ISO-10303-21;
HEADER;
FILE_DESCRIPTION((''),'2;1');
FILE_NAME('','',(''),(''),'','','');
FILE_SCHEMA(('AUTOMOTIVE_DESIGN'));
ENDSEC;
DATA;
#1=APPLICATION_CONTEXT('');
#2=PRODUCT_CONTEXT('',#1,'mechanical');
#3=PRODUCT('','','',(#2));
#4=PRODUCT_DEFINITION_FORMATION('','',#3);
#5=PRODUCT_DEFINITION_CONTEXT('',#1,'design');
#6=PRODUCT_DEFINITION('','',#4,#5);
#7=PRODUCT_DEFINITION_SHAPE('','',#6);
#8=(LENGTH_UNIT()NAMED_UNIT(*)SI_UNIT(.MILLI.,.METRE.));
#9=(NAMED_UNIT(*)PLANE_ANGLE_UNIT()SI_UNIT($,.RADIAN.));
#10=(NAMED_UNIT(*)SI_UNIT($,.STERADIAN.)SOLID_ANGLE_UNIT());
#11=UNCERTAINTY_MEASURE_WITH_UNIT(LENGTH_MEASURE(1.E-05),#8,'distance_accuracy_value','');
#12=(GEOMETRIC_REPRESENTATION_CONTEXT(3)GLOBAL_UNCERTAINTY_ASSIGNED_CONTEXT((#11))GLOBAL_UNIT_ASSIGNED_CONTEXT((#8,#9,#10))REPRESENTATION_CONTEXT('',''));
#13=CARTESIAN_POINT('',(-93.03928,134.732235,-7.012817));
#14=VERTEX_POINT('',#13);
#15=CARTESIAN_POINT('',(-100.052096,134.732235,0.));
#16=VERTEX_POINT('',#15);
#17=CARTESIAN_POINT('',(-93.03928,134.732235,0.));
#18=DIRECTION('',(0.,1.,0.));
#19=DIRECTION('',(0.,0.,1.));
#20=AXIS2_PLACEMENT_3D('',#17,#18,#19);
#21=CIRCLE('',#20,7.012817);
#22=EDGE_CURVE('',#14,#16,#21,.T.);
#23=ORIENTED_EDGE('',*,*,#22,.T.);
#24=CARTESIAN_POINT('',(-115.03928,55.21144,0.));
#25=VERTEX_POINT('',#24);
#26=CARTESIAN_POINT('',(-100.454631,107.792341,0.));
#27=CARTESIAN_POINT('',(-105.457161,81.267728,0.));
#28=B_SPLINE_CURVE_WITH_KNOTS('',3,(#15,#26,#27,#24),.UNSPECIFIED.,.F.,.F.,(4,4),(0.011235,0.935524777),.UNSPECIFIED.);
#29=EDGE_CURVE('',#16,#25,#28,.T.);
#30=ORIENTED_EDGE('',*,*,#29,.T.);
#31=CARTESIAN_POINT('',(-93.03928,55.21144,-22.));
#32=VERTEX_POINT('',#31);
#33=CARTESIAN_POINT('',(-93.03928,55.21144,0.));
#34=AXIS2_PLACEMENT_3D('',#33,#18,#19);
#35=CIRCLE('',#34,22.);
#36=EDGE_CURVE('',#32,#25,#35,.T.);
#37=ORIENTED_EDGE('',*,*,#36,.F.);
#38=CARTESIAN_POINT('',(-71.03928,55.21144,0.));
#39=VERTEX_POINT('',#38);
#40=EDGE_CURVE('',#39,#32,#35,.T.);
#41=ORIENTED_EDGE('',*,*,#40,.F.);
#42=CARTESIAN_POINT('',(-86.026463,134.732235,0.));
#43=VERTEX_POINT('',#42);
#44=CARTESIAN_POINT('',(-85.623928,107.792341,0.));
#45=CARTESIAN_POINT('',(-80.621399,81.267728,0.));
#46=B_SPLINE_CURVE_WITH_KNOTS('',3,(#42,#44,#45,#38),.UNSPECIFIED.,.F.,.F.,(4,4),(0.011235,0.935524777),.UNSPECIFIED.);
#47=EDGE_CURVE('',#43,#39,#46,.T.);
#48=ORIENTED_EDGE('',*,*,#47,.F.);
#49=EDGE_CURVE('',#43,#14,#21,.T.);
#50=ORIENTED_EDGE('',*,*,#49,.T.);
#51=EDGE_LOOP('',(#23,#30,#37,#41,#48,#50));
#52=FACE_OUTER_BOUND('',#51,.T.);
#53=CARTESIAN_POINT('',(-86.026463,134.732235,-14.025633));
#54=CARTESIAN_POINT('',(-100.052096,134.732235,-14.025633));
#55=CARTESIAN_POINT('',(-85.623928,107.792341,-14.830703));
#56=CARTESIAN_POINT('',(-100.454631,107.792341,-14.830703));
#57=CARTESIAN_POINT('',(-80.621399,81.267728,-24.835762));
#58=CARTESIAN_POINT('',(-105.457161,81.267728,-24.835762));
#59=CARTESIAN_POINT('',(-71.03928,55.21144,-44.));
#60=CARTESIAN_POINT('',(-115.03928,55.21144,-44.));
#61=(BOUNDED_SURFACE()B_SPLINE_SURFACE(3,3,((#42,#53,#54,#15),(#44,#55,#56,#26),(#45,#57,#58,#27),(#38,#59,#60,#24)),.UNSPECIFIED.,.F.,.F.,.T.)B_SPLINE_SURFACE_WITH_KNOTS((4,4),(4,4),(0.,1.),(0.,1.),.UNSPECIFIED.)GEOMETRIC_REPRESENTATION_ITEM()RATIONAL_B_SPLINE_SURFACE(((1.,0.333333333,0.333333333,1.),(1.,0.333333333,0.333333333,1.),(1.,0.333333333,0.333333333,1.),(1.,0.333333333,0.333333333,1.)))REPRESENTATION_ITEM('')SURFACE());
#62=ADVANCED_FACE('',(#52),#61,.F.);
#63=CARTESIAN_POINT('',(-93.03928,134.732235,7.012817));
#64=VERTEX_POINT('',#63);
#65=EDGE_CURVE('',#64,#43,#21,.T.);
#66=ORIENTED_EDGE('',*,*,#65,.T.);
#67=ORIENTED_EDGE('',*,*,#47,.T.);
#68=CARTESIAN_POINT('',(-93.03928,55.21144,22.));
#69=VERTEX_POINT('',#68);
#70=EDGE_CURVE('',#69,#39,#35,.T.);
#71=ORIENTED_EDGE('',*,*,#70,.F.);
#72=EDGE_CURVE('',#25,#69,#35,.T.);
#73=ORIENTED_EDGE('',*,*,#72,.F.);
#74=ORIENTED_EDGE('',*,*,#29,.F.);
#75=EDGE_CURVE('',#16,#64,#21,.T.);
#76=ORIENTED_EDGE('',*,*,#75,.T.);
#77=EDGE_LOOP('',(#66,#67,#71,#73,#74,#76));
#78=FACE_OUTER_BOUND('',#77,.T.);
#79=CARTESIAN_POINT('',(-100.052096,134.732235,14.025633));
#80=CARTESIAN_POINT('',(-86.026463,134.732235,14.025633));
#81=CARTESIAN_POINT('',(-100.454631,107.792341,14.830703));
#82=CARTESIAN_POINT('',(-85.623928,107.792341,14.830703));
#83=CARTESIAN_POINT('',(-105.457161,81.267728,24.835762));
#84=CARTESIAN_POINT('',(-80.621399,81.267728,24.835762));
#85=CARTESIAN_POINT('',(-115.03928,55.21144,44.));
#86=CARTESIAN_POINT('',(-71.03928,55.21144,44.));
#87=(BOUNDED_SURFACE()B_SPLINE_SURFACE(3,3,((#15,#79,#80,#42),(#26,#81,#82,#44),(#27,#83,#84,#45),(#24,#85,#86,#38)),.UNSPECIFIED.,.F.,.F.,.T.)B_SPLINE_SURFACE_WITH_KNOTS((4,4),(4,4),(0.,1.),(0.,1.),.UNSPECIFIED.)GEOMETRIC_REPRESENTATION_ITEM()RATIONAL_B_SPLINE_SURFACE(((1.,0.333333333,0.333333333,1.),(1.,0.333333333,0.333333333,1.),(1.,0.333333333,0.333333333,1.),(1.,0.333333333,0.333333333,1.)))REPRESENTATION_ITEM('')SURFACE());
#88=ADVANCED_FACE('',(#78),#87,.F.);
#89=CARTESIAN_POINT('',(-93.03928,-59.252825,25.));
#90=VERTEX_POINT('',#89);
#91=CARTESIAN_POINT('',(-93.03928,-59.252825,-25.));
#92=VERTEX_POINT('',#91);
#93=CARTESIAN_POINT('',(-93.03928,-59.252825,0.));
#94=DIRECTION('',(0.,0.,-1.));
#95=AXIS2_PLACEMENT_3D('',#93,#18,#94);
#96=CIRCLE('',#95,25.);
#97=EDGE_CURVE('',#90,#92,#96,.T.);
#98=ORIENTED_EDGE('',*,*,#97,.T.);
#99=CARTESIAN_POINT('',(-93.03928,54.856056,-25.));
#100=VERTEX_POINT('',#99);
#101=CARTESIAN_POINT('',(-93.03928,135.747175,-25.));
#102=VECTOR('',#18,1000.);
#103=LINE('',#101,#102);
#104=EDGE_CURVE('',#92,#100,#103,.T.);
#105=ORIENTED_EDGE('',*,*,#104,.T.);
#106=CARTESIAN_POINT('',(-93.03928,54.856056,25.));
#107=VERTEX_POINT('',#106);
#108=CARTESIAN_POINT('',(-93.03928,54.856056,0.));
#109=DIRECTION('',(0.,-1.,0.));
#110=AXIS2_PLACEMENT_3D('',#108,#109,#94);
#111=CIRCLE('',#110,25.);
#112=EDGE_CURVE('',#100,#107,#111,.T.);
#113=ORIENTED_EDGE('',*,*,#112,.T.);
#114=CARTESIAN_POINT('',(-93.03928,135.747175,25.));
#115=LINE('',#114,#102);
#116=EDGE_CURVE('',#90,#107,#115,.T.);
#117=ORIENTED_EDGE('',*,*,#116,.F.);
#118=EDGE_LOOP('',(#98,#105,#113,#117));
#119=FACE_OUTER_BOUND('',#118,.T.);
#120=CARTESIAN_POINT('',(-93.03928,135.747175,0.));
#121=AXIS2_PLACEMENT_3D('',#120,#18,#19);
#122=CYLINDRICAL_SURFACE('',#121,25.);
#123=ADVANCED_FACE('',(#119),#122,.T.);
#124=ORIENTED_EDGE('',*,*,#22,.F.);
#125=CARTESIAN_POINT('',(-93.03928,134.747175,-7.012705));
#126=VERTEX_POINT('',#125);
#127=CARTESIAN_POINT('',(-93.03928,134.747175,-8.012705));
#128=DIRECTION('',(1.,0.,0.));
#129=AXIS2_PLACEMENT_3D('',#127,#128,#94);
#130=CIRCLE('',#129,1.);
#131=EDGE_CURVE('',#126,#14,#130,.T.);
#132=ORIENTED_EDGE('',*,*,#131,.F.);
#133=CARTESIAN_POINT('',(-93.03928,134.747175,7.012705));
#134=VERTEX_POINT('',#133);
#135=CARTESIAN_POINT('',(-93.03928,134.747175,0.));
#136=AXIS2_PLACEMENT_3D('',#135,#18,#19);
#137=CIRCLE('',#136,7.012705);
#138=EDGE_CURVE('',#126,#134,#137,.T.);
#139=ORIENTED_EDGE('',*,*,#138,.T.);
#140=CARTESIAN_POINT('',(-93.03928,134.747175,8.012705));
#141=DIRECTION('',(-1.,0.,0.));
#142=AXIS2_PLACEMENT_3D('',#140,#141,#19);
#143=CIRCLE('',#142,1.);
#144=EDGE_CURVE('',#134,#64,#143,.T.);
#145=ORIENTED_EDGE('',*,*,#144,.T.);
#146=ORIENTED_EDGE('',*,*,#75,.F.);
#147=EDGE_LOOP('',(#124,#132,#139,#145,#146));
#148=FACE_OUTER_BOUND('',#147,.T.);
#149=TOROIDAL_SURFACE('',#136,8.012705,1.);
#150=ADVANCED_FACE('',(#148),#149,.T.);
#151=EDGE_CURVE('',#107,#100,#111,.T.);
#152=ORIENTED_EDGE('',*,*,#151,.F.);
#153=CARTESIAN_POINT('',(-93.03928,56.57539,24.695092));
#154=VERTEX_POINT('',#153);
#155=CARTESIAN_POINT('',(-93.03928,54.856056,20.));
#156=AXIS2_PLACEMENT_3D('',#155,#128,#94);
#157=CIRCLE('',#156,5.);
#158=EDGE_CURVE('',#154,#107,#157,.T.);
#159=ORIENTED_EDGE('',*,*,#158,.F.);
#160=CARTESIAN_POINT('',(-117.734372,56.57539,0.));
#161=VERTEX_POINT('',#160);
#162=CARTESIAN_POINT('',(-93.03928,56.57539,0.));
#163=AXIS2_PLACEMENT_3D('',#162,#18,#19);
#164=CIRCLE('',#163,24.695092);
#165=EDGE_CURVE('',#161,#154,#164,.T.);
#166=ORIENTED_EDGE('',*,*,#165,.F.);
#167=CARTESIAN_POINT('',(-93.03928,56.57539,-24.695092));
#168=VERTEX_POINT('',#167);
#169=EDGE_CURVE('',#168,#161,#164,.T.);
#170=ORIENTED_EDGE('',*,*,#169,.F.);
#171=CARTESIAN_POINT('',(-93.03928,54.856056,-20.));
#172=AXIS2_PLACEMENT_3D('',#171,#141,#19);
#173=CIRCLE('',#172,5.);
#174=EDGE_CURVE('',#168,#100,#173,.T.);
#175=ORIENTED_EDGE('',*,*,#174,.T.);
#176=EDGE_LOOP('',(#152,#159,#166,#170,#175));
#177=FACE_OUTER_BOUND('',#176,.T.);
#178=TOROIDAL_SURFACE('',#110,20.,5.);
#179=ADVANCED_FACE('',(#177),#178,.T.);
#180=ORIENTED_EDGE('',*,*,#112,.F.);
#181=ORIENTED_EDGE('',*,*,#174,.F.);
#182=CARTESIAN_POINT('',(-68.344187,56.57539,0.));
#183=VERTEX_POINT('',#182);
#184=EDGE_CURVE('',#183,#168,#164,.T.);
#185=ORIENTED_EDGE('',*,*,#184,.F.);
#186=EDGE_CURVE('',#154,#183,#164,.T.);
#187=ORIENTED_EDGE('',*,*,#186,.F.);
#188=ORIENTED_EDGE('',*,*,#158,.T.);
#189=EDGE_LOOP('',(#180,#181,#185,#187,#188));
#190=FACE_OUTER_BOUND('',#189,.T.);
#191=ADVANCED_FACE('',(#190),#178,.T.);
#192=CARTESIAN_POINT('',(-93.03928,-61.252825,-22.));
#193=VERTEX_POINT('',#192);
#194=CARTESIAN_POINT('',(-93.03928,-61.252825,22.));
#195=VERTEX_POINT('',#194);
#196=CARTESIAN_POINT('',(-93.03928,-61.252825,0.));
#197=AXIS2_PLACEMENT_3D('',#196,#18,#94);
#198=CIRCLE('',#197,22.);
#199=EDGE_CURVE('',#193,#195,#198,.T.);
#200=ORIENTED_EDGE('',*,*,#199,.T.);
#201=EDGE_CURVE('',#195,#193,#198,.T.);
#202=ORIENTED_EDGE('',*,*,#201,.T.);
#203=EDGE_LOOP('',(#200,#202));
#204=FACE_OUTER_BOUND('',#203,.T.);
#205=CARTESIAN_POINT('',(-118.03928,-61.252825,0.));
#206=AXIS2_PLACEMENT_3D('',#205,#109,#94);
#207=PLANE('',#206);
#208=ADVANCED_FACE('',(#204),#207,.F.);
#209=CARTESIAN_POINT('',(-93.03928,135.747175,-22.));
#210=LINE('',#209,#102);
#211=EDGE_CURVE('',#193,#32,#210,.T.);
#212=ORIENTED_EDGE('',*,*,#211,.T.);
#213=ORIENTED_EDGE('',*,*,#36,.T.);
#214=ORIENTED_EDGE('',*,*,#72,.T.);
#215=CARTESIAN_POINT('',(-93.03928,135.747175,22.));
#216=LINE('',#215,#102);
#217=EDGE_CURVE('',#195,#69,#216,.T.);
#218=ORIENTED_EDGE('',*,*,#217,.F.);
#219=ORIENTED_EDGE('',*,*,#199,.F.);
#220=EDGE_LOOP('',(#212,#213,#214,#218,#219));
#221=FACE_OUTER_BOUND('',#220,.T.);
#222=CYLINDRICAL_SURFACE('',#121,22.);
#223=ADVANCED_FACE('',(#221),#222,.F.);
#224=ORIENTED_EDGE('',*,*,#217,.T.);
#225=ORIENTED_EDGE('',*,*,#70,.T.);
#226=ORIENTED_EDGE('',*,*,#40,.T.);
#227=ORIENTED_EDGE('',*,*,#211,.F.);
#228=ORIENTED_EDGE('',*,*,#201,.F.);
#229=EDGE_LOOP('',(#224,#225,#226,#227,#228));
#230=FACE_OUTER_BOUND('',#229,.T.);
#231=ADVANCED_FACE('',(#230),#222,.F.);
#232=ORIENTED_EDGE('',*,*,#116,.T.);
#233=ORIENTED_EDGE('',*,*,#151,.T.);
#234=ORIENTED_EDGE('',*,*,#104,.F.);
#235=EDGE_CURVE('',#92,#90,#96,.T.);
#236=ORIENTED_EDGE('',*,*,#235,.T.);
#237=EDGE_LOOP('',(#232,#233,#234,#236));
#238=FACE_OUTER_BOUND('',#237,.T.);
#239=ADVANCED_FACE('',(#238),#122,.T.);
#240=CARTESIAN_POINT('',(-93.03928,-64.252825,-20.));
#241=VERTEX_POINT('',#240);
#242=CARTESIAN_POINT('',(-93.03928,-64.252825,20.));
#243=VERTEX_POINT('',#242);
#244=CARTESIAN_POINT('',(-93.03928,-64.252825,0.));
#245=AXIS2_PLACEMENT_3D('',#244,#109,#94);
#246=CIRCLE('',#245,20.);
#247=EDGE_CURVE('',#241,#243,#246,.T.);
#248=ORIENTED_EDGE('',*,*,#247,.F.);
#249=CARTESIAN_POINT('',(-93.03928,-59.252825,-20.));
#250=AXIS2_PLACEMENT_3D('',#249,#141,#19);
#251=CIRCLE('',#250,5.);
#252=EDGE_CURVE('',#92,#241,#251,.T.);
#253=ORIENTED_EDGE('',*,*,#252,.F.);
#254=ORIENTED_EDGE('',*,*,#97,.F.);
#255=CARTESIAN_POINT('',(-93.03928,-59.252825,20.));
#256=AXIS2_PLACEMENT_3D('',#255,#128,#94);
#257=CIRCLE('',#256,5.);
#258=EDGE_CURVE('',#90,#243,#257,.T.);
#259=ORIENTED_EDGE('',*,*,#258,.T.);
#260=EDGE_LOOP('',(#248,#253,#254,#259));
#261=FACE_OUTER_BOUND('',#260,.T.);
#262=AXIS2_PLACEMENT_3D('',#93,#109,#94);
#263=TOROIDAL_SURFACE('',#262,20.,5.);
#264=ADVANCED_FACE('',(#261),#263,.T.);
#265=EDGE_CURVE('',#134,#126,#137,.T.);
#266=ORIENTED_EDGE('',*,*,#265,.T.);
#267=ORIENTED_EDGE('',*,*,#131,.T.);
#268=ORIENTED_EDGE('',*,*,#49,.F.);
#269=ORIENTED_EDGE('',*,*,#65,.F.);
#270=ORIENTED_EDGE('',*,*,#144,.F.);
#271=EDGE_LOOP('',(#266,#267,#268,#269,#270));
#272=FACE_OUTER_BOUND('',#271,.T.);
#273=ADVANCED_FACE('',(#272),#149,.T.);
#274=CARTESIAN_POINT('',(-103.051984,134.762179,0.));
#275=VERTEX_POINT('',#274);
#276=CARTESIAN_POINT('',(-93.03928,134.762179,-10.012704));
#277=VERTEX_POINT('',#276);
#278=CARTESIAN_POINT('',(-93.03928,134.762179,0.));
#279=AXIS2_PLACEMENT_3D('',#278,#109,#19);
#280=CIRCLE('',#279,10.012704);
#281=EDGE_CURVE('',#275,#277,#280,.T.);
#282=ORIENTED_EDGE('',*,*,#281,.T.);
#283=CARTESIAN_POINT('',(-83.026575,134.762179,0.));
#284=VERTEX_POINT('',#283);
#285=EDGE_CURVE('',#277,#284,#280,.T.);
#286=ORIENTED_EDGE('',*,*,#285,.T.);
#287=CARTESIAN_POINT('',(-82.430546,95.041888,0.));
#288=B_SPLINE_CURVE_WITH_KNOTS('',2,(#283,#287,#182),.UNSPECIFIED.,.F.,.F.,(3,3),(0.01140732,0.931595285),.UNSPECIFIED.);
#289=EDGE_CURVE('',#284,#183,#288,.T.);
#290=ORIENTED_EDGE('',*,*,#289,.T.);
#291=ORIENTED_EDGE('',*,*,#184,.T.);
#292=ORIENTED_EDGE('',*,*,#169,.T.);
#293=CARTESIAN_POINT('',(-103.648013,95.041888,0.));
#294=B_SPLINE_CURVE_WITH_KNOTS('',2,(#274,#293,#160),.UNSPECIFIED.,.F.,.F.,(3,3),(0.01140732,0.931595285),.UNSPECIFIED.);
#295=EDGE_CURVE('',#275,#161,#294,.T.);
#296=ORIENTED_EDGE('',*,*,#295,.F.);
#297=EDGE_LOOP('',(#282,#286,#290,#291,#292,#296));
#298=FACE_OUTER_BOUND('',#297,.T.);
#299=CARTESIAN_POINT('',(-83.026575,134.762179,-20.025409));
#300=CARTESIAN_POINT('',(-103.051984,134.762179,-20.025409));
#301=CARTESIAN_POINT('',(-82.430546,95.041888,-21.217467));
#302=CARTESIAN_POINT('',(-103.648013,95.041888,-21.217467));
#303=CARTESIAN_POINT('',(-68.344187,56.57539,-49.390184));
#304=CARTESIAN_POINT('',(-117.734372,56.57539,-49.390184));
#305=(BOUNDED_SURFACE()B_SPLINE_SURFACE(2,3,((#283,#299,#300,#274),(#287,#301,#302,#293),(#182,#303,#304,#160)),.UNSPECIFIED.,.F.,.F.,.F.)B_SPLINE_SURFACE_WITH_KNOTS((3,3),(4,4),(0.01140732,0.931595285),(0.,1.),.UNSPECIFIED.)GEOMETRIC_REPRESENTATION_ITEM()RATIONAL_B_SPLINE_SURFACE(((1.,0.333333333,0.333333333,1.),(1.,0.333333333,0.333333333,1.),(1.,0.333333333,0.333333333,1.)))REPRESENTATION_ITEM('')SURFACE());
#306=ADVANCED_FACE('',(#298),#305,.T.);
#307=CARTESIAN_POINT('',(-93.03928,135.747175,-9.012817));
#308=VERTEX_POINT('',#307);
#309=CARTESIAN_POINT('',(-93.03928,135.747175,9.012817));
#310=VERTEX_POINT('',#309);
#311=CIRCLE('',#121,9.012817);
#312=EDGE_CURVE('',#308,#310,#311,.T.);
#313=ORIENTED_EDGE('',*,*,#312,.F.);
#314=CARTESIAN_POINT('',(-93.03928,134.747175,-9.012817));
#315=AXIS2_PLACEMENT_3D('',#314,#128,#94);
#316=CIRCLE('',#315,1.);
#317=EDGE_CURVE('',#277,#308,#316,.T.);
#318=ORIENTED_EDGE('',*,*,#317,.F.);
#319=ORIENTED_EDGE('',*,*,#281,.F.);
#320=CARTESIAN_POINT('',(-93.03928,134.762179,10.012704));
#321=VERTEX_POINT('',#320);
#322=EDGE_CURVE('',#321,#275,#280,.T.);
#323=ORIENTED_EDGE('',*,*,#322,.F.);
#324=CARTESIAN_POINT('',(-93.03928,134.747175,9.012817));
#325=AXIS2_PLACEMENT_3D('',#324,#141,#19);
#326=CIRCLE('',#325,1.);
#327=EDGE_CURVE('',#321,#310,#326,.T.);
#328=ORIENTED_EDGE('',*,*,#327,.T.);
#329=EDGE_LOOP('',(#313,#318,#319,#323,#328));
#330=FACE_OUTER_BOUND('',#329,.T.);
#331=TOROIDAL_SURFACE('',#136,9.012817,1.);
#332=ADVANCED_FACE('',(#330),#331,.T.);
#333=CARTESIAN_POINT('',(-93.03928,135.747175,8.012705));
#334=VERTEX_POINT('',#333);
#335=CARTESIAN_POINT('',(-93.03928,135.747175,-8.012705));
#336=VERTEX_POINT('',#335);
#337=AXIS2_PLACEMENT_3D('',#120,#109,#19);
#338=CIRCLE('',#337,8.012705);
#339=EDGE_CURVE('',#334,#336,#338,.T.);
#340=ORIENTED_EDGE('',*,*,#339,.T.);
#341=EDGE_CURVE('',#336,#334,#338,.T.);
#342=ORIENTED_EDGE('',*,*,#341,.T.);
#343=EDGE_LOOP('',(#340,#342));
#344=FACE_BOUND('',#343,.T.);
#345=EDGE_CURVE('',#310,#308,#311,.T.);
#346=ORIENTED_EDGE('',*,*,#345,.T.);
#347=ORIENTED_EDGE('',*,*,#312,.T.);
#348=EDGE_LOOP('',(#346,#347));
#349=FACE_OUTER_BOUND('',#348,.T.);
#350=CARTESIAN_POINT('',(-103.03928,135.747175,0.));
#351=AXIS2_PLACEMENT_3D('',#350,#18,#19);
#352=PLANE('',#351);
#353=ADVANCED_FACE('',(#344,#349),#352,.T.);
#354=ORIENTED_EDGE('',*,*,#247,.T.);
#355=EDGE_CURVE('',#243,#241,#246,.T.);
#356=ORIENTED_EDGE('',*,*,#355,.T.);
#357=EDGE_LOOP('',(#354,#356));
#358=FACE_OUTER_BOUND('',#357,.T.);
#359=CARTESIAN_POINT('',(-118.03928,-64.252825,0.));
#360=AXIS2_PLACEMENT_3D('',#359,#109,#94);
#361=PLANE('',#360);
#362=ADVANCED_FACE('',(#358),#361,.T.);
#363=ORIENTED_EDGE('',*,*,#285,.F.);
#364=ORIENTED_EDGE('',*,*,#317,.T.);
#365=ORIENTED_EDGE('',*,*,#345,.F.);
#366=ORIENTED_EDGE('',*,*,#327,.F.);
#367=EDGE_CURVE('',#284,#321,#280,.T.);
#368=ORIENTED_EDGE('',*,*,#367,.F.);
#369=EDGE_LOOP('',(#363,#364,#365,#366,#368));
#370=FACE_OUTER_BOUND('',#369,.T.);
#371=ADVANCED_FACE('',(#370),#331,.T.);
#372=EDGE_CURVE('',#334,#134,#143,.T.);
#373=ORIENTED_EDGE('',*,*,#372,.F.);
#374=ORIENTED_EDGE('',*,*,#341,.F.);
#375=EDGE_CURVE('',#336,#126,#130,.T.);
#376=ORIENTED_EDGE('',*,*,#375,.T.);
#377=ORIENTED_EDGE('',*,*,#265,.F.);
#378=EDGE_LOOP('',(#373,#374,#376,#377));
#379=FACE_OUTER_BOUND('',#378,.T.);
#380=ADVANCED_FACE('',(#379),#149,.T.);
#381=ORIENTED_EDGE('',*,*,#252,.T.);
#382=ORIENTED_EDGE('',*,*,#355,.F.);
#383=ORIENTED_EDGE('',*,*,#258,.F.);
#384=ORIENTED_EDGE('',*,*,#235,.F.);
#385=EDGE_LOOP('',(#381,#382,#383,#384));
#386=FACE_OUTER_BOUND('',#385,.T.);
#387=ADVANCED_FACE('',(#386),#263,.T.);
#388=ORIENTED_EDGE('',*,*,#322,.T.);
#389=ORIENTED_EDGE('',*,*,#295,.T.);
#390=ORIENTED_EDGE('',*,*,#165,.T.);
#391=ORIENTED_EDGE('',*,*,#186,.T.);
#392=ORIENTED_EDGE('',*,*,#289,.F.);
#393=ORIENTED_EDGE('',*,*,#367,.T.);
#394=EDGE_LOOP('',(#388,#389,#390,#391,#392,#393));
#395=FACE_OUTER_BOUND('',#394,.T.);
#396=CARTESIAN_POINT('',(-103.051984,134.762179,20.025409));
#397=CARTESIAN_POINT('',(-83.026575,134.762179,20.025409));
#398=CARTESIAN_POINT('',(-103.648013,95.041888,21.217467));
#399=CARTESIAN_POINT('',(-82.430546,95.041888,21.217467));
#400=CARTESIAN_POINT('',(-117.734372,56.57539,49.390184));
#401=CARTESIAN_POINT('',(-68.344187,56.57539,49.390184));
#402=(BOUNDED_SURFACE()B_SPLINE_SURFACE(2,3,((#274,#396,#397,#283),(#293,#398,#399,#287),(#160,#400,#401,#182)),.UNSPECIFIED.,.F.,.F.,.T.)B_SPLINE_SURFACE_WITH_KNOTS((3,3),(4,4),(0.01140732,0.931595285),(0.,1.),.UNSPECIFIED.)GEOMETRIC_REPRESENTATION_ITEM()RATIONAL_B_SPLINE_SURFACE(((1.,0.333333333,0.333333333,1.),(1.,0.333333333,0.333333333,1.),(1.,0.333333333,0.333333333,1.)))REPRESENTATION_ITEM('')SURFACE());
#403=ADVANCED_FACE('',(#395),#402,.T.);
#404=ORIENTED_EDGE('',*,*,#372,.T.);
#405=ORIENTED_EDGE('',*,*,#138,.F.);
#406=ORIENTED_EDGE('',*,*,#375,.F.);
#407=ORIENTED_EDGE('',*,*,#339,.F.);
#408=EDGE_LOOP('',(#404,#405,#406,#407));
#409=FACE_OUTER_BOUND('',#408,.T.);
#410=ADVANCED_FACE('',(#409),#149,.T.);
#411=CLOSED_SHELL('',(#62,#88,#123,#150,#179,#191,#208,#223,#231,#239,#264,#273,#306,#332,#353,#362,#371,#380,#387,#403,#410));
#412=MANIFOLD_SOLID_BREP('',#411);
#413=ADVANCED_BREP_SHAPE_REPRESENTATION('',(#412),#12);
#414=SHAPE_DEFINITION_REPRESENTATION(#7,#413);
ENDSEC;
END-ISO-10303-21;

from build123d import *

# Parameters (mm, degrees)
SHELL1_T  = -3
FILLET1_R = 5
FILLET2_R = 1


with BuildPart() as part:
    # Sketch1 → Revolve1 (revolve)
    with BuildSketch(Plane.XY, mode=Mode.PRIVATE) as revolve1_sk:
        with BuildLine():
            Line((-93.039279644, 135.747175363), (-93.039279644, -64.252824637))
            Line((-93.039279644, -64.252824637), (-118.039279644, -64.252824637))
            Line((-118.039279644, -64.252824637), (-118.039279644, 55.747175363))
            add(Edge.make_bspline(
                [(-118.039279644, 55.747175363), (-103.478005536, 95.090899145), (-103.039279644, 135.747175363)],
                knots=[0, 0, 0, 0.941503214, 0.941503214, 0.941503214], degree=2))
            Line((-103.039279644, 135.747175363), (-93.039279644, 135.747175363))
        make_face()
    revolve(revolve1_sk.sketch.rotate(Axis((-93.039279644, 135.747175363, 0), (0, -1, 0)), 270), axis=Axis((-93.039279644, 135.747175363, 0), (0, -1, 0)))

    # Shell1
    shell1_openings = [part.faces().sort_by_distance(p)[0] for p in [
        (-93.039279644, 135.747175363, 0),
    ]]
    offset(amount=SHELL1_T, openings=shell1_openings, kind=Kind.INTERSECTION)

    # Fillet1
    fillet1_edges = [part.edges().sort_by_distance(p)[0] for p in [
        (-93.039279644, 55.747175363, -25),
        (-93.039279644, -64.252824637, -25),
    ]]
    fillet(fillet1_edges, radius=FILLET1_R)

    # Fillet2
    fillet2_edges = [part.edges().sort_by_distance(p)[0] for p in [
        (-93.039279644, 135.747175363, -6.999825357),
        (-93.039279644, 135.747175363, -10),
    ]]
    fillet(fillet2_edges, radius=FILLET2_R)


solid = part.part
